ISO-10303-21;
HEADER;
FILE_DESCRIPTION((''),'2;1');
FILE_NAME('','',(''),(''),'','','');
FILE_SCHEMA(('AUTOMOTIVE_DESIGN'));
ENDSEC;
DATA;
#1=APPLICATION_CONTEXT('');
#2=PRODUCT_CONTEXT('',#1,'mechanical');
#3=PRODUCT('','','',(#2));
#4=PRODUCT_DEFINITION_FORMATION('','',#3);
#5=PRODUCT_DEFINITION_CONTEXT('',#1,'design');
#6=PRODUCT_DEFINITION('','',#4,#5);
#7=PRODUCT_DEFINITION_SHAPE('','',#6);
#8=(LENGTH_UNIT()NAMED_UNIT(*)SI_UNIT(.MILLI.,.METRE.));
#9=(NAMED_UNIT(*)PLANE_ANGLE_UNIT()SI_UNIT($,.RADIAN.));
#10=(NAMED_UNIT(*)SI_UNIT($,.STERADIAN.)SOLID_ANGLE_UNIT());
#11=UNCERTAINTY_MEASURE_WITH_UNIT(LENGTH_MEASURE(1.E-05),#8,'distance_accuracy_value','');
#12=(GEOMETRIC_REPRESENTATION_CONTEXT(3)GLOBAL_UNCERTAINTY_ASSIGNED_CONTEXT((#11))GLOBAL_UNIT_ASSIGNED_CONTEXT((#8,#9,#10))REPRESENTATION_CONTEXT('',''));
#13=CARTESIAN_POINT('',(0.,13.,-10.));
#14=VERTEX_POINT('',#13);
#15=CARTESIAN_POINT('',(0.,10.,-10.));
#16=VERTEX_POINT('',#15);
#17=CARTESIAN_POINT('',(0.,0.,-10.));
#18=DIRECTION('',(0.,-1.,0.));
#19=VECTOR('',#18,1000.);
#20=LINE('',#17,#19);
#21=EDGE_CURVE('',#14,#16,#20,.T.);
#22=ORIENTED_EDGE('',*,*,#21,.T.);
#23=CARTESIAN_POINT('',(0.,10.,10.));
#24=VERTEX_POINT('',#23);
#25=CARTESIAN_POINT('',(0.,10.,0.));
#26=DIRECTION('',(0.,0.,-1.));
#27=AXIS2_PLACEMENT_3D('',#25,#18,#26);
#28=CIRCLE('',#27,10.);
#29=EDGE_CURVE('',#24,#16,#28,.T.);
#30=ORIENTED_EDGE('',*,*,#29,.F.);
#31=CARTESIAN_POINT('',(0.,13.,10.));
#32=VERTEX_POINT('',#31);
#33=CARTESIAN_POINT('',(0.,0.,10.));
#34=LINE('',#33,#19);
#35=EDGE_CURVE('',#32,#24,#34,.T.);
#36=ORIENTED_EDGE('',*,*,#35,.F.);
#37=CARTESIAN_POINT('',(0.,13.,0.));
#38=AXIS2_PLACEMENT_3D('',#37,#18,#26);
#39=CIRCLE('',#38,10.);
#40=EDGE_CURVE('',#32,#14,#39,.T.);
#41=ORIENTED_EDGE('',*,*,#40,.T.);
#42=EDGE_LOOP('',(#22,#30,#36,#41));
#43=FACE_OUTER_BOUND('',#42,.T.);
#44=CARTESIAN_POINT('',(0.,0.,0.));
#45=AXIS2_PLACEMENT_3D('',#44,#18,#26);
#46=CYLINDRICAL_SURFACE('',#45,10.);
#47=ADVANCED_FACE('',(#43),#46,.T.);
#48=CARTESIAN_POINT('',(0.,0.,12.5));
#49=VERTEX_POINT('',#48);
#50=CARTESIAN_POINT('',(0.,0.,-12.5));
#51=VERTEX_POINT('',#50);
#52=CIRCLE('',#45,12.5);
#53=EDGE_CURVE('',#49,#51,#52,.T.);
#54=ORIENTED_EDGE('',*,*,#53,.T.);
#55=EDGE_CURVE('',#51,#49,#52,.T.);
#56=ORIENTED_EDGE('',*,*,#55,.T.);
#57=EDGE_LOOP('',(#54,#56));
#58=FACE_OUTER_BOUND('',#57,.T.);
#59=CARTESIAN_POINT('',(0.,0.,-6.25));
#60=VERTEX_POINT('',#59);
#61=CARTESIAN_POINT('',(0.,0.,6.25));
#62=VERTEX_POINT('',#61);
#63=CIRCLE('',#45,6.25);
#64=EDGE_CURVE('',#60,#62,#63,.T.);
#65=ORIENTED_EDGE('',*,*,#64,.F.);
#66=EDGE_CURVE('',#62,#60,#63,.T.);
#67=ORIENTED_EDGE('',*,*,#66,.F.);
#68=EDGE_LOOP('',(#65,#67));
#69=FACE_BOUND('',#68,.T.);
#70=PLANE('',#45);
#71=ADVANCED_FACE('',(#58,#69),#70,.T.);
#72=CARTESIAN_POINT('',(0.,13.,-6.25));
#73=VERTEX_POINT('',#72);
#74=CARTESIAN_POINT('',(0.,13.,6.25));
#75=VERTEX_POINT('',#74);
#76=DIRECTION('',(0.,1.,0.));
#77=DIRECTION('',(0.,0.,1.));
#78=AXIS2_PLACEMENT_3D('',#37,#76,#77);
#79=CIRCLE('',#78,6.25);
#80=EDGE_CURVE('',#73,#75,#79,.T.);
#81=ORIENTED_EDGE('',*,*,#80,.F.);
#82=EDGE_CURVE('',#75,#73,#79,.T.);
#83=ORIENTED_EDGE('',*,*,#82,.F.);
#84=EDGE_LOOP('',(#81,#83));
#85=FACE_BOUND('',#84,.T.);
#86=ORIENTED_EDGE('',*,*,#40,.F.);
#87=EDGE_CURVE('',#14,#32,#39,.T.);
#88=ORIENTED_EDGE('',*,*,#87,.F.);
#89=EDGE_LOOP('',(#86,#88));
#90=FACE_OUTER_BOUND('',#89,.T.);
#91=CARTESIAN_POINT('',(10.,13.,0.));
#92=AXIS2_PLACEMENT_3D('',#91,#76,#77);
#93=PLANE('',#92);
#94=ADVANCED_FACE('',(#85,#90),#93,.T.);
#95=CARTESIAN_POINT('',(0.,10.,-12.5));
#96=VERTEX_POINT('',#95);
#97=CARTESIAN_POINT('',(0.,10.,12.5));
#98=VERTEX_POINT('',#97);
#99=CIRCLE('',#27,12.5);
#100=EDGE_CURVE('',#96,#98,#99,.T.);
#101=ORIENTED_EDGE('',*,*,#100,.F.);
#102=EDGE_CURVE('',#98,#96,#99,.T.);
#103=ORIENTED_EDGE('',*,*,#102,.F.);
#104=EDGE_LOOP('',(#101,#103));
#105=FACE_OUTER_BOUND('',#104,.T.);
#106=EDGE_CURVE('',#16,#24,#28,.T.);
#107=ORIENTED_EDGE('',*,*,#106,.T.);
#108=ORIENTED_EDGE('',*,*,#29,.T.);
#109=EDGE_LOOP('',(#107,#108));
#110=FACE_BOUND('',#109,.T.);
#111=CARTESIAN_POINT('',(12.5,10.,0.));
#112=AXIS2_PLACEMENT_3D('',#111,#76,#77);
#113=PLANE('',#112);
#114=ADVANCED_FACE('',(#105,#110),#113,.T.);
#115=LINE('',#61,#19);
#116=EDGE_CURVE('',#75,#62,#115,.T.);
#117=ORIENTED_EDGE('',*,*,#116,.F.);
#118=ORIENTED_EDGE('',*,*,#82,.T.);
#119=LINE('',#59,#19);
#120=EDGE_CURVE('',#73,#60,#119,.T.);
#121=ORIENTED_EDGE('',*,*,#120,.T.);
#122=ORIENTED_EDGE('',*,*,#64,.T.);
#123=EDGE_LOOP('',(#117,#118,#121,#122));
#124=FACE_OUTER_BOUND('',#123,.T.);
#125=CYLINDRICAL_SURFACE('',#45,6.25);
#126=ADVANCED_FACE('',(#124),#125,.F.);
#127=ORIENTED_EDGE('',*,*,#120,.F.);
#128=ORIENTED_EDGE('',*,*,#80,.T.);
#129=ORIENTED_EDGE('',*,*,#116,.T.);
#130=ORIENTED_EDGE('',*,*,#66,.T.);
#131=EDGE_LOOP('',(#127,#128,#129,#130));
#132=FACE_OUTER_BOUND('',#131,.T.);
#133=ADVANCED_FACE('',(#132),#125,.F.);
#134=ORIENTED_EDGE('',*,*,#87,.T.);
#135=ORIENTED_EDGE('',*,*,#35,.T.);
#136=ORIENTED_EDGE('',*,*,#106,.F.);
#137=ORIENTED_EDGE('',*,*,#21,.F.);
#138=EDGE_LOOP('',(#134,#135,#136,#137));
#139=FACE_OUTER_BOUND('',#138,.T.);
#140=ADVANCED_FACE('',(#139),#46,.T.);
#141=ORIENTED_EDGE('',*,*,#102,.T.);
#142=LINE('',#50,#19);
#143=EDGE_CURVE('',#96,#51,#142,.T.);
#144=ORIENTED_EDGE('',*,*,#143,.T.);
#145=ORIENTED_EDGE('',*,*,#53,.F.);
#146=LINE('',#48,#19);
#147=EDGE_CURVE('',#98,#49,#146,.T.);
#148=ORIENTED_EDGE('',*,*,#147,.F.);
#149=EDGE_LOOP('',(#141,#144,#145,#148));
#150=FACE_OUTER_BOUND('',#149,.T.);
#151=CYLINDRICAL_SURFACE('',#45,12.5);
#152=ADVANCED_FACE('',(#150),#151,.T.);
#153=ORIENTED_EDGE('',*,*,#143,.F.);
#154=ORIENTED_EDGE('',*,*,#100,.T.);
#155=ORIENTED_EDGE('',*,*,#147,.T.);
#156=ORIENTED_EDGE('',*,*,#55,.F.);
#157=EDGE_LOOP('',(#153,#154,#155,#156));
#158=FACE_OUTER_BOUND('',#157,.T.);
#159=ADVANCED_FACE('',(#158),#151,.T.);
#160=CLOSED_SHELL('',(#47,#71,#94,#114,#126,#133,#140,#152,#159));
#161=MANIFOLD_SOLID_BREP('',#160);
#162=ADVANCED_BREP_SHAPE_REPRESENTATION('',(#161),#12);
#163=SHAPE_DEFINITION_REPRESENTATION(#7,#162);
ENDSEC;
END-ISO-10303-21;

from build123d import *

# Parameters (mm, degrees)
M14X1_5_TAPPED_HOLE1_D     = 12.5
M14X1_5_TAPPED_HOLE1_DEPTH = 35.5
M14X1_5_TAPPED_HOLE1_TIP   = 3.755378869


with BuildPart() as part:
    # Sketch1 → Revolve1 (revolve)
    with BuildSketch(Plane.XY, mode=Mode.PRIVATE) as revolve1_sk:
        Polygon((0, 0), (12.5, 0), (12.5, 10), (10, 10), (10, 13), (0, 13), align=None)
    revolve(revolve1_sk.sketch.rotate(Axis((0, 0, 0), (0, 1, 0)), 90), axis=Axis((0, 0, 0), (0, 1, 0)))

    # M14x1.5 Tapped Hole1
    with Locations(Plane(origin=(0, 0, 0), x_dir=(-1, 0, 0), z_dir=(0, -1, 0))):
        with Locations((0, 0)):
            Hole(M14X1_5_TAPPED_HOLE1_D / 2, depth=M14X1_5_TAPPED_HOLE1_DEPTH)
            with Locations((0, 0, -(M14X1_5_TAPPED_HOLE1_DEPTH + M14X1_5_TAPPED_HOLE1_TIP / 2))):  # 118° drill point
                Cone(0, M14X1_5_TAPPED_HOLE1_D / 2, M14X1_5_TAPPED_HOLE1_TIP, mode=Mode.SUBTRACT)


solid = part.part
